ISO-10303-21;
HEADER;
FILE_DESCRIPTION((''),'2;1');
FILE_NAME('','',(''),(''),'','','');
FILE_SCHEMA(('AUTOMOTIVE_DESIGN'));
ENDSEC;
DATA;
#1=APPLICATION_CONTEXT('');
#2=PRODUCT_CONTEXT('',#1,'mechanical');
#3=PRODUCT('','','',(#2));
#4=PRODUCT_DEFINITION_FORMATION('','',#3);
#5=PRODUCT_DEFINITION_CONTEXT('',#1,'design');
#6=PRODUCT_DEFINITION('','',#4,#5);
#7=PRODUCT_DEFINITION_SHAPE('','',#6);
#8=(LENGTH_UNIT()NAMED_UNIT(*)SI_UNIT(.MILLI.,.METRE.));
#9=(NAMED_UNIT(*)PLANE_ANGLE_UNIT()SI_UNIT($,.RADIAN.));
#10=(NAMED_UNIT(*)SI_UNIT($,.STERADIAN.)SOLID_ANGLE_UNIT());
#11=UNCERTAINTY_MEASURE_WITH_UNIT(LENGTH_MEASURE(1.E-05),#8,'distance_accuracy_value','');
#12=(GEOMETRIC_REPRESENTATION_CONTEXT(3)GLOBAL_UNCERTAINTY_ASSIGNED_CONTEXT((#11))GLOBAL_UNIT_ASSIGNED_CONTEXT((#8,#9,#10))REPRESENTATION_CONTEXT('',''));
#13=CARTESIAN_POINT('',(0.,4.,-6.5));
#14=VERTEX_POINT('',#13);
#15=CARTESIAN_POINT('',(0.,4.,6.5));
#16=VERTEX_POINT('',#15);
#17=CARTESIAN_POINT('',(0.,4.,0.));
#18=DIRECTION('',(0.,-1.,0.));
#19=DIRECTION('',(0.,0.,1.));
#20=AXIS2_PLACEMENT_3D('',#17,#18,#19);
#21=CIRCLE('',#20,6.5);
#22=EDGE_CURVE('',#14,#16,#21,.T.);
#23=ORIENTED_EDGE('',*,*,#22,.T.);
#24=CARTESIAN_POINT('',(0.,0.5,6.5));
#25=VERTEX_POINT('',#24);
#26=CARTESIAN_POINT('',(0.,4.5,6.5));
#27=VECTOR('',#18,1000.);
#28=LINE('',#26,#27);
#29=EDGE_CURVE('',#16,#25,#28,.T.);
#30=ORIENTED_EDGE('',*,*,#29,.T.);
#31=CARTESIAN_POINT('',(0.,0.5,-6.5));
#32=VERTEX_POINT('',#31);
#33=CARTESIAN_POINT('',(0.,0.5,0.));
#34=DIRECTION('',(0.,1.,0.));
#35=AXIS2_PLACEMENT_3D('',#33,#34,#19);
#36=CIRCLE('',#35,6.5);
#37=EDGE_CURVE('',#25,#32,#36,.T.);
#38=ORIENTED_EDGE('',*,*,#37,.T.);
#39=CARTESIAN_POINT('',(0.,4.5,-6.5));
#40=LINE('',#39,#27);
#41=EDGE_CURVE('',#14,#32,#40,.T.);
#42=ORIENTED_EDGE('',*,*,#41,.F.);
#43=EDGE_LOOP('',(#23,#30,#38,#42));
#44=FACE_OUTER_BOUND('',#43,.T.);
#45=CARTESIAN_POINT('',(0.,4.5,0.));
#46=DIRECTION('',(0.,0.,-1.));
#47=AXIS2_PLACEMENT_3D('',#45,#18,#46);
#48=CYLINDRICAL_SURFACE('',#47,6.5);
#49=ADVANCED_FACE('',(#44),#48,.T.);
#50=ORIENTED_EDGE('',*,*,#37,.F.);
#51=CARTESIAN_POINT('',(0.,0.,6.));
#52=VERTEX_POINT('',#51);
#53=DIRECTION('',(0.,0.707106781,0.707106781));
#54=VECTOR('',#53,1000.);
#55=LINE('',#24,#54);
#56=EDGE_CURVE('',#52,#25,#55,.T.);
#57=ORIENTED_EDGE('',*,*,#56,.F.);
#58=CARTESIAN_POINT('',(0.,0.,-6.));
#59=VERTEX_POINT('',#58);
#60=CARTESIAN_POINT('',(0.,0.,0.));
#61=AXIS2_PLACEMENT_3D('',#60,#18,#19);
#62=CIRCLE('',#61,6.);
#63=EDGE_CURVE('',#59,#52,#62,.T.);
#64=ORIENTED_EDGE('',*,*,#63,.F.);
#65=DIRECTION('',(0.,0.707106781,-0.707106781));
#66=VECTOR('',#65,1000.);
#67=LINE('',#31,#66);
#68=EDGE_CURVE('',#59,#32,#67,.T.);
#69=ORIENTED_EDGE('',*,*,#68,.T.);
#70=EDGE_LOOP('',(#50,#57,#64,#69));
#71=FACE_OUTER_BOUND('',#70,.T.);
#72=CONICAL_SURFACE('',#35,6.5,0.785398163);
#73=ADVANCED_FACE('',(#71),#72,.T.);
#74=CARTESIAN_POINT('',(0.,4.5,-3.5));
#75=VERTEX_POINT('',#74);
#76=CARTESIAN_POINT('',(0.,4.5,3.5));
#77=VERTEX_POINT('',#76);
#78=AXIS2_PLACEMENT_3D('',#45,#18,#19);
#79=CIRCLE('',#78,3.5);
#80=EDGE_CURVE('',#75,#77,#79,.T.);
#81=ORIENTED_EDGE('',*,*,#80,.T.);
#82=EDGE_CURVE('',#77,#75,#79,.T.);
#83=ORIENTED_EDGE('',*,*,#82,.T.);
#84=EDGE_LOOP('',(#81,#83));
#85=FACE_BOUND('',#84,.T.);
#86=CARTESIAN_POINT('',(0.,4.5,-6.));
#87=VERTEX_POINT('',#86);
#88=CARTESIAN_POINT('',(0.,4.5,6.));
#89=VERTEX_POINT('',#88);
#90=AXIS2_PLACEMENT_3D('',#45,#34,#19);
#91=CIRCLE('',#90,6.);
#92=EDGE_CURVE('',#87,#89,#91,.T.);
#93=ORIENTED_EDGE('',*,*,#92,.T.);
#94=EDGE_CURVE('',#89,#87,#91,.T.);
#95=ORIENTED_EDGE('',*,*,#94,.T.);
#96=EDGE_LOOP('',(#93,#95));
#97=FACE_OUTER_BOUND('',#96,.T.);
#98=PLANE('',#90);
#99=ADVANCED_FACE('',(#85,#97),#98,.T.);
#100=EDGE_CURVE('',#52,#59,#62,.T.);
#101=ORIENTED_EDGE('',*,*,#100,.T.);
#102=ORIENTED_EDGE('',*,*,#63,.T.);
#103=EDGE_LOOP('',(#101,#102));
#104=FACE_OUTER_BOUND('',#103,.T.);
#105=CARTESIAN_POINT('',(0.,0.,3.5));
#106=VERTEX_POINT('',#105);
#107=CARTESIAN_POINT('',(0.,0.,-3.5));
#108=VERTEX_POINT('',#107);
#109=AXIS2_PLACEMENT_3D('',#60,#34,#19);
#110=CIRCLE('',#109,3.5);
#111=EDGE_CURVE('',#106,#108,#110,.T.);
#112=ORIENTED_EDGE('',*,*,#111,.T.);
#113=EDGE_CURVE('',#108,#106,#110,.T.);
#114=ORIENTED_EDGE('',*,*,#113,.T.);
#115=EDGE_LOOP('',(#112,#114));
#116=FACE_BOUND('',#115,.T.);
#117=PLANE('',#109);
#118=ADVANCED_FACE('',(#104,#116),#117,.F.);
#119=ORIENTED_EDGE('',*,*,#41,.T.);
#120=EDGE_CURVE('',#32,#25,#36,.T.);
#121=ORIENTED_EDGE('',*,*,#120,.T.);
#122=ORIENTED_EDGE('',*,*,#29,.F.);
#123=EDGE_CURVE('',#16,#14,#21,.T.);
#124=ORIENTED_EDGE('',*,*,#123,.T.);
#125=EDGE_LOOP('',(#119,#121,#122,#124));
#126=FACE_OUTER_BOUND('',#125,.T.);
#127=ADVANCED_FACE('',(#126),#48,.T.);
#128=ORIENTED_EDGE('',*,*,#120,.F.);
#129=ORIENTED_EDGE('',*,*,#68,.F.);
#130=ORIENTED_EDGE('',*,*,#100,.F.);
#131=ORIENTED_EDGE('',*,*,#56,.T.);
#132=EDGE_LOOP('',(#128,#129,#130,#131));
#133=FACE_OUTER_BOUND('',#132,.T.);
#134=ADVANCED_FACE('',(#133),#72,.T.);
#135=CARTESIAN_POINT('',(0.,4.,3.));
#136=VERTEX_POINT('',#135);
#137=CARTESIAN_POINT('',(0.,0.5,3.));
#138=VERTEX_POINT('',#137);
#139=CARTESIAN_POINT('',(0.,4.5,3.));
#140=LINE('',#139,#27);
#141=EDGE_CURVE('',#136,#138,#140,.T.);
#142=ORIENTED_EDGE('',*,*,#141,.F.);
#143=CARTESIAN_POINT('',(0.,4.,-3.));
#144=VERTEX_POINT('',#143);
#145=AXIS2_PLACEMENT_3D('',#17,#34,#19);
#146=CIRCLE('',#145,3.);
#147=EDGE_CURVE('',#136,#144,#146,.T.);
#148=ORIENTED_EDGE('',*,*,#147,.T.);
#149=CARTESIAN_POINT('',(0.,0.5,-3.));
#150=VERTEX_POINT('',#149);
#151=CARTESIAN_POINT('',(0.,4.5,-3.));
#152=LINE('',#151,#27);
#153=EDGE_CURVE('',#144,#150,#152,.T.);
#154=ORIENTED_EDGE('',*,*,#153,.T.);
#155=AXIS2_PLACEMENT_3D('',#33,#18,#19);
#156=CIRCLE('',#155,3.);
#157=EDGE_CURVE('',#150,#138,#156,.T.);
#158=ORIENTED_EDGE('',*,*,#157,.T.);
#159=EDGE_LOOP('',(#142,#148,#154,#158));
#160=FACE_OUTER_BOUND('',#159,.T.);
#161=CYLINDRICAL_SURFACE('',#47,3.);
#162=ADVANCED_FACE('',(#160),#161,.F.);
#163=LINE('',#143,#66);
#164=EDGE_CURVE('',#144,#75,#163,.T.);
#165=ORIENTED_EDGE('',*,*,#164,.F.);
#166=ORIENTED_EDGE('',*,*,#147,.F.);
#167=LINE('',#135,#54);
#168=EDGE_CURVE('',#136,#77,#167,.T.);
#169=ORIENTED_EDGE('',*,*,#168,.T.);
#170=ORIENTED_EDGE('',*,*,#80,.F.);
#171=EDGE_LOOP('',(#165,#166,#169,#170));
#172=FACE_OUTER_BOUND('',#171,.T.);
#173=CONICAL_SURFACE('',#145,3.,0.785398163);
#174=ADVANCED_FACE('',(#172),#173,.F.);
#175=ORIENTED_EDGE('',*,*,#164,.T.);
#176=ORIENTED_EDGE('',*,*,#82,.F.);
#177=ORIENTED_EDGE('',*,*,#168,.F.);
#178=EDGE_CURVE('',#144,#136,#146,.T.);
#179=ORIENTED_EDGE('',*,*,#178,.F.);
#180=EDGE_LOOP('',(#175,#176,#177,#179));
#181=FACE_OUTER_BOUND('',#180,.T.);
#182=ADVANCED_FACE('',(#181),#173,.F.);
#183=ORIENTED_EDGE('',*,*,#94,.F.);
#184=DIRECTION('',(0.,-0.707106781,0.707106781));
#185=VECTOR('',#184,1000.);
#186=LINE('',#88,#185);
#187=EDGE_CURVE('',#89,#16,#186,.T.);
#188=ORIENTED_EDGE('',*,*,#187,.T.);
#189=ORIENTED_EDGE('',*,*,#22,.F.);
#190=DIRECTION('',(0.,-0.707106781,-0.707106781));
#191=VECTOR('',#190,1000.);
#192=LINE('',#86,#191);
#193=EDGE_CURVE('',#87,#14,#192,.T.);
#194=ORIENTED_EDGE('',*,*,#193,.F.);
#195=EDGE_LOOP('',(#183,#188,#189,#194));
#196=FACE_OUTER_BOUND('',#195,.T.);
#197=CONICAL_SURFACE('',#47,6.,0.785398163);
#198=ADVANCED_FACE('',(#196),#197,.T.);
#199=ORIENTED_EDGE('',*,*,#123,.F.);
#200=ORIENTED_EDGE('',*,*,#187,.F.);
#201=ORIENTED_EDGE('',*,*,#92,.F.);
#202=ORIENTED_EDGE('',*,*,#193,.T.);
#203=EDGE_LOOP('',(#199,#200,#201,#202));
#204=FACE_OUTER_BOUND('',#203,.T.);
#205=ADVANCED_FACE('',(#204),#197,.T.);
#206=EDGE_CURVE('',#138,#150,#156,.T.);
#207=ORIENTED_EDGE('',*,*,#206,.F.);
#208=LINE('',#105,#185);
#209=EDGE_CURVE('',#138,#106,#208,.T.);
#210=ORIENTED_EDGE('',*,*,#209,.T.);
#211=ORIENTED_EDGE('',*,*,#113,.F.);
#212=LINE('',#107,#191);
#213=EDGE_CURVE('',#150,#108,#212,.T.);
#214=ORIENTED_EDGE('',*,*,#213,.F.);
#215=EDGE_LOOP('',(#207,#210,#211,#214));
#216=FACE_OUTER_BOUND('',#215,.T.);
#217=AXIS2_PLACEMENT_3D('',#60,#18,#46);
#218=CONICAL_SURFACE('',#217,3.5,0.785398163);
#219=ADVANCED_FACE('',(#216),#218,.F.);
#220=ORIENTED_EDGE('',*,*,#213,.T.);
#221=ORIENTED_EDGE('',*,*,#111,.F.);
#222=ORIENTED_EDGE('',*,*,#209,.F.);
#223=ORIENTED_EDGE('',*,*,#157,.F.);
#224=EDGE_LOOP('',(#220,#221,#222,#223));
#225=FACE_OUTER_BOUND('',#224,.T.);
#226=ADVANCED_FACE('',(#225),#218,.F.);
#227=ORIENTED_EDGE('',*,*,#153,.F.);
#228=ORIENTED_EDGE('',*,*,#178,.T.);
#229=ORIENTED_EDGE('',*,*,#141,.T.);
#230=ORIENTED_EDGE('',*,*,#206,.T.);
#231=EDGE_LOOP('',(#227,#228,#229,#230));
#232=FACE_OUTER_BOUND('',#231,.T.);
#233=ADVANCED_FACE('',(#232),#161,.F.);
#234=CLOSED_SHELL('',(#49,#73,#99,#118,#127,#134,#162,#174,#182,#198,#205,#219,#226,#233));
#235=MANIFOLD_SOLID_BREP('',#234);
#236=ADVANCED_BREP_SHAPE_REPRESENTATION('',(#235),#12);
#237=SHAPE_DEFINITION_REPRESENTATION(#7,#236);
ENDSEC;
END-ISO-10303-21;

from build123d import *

# Parameters (mm, degrees)
SKETCH1_R           = 6.5
SKETCH1_R_2         = 3
BOSS_EXTRUDE1_DEPTH = 4.5
CHAMFER1_SIZE       = 0.5


with BuildPart() as part:
    # Sketch1 → Boss-Extrude1 (new body)
    with BuildSketch(Plane(origin=(0, 0, 0), x_dir=(1, 0, 0), z_dir=(0, 1, 0))):
        with Locations(Location((0, 0, 0), (0, 0, 270))):
            Circle(SKETCH1_R)
        with Locations(Location((0, 0, 0), (0, 0, 270))):
            Circle(SKETCH1_R_2, mode=Mode.SUBTRACT)
    extrude(amount=BOSS_EXTRUDE1_DEPTH)

    # Chamfer1
    chamfer1_edges = [part.edges().sort_by_distance(p)[0] for p in [
        (0, 0, -6.5),
        (0, 4.5, -6.5),
        (0, 0, -3),
        (0, 4.5, -3),
    ]]
    chamfer(chamfer1_edges, length=CHAMFER1_SIZE)


solid = part.part
